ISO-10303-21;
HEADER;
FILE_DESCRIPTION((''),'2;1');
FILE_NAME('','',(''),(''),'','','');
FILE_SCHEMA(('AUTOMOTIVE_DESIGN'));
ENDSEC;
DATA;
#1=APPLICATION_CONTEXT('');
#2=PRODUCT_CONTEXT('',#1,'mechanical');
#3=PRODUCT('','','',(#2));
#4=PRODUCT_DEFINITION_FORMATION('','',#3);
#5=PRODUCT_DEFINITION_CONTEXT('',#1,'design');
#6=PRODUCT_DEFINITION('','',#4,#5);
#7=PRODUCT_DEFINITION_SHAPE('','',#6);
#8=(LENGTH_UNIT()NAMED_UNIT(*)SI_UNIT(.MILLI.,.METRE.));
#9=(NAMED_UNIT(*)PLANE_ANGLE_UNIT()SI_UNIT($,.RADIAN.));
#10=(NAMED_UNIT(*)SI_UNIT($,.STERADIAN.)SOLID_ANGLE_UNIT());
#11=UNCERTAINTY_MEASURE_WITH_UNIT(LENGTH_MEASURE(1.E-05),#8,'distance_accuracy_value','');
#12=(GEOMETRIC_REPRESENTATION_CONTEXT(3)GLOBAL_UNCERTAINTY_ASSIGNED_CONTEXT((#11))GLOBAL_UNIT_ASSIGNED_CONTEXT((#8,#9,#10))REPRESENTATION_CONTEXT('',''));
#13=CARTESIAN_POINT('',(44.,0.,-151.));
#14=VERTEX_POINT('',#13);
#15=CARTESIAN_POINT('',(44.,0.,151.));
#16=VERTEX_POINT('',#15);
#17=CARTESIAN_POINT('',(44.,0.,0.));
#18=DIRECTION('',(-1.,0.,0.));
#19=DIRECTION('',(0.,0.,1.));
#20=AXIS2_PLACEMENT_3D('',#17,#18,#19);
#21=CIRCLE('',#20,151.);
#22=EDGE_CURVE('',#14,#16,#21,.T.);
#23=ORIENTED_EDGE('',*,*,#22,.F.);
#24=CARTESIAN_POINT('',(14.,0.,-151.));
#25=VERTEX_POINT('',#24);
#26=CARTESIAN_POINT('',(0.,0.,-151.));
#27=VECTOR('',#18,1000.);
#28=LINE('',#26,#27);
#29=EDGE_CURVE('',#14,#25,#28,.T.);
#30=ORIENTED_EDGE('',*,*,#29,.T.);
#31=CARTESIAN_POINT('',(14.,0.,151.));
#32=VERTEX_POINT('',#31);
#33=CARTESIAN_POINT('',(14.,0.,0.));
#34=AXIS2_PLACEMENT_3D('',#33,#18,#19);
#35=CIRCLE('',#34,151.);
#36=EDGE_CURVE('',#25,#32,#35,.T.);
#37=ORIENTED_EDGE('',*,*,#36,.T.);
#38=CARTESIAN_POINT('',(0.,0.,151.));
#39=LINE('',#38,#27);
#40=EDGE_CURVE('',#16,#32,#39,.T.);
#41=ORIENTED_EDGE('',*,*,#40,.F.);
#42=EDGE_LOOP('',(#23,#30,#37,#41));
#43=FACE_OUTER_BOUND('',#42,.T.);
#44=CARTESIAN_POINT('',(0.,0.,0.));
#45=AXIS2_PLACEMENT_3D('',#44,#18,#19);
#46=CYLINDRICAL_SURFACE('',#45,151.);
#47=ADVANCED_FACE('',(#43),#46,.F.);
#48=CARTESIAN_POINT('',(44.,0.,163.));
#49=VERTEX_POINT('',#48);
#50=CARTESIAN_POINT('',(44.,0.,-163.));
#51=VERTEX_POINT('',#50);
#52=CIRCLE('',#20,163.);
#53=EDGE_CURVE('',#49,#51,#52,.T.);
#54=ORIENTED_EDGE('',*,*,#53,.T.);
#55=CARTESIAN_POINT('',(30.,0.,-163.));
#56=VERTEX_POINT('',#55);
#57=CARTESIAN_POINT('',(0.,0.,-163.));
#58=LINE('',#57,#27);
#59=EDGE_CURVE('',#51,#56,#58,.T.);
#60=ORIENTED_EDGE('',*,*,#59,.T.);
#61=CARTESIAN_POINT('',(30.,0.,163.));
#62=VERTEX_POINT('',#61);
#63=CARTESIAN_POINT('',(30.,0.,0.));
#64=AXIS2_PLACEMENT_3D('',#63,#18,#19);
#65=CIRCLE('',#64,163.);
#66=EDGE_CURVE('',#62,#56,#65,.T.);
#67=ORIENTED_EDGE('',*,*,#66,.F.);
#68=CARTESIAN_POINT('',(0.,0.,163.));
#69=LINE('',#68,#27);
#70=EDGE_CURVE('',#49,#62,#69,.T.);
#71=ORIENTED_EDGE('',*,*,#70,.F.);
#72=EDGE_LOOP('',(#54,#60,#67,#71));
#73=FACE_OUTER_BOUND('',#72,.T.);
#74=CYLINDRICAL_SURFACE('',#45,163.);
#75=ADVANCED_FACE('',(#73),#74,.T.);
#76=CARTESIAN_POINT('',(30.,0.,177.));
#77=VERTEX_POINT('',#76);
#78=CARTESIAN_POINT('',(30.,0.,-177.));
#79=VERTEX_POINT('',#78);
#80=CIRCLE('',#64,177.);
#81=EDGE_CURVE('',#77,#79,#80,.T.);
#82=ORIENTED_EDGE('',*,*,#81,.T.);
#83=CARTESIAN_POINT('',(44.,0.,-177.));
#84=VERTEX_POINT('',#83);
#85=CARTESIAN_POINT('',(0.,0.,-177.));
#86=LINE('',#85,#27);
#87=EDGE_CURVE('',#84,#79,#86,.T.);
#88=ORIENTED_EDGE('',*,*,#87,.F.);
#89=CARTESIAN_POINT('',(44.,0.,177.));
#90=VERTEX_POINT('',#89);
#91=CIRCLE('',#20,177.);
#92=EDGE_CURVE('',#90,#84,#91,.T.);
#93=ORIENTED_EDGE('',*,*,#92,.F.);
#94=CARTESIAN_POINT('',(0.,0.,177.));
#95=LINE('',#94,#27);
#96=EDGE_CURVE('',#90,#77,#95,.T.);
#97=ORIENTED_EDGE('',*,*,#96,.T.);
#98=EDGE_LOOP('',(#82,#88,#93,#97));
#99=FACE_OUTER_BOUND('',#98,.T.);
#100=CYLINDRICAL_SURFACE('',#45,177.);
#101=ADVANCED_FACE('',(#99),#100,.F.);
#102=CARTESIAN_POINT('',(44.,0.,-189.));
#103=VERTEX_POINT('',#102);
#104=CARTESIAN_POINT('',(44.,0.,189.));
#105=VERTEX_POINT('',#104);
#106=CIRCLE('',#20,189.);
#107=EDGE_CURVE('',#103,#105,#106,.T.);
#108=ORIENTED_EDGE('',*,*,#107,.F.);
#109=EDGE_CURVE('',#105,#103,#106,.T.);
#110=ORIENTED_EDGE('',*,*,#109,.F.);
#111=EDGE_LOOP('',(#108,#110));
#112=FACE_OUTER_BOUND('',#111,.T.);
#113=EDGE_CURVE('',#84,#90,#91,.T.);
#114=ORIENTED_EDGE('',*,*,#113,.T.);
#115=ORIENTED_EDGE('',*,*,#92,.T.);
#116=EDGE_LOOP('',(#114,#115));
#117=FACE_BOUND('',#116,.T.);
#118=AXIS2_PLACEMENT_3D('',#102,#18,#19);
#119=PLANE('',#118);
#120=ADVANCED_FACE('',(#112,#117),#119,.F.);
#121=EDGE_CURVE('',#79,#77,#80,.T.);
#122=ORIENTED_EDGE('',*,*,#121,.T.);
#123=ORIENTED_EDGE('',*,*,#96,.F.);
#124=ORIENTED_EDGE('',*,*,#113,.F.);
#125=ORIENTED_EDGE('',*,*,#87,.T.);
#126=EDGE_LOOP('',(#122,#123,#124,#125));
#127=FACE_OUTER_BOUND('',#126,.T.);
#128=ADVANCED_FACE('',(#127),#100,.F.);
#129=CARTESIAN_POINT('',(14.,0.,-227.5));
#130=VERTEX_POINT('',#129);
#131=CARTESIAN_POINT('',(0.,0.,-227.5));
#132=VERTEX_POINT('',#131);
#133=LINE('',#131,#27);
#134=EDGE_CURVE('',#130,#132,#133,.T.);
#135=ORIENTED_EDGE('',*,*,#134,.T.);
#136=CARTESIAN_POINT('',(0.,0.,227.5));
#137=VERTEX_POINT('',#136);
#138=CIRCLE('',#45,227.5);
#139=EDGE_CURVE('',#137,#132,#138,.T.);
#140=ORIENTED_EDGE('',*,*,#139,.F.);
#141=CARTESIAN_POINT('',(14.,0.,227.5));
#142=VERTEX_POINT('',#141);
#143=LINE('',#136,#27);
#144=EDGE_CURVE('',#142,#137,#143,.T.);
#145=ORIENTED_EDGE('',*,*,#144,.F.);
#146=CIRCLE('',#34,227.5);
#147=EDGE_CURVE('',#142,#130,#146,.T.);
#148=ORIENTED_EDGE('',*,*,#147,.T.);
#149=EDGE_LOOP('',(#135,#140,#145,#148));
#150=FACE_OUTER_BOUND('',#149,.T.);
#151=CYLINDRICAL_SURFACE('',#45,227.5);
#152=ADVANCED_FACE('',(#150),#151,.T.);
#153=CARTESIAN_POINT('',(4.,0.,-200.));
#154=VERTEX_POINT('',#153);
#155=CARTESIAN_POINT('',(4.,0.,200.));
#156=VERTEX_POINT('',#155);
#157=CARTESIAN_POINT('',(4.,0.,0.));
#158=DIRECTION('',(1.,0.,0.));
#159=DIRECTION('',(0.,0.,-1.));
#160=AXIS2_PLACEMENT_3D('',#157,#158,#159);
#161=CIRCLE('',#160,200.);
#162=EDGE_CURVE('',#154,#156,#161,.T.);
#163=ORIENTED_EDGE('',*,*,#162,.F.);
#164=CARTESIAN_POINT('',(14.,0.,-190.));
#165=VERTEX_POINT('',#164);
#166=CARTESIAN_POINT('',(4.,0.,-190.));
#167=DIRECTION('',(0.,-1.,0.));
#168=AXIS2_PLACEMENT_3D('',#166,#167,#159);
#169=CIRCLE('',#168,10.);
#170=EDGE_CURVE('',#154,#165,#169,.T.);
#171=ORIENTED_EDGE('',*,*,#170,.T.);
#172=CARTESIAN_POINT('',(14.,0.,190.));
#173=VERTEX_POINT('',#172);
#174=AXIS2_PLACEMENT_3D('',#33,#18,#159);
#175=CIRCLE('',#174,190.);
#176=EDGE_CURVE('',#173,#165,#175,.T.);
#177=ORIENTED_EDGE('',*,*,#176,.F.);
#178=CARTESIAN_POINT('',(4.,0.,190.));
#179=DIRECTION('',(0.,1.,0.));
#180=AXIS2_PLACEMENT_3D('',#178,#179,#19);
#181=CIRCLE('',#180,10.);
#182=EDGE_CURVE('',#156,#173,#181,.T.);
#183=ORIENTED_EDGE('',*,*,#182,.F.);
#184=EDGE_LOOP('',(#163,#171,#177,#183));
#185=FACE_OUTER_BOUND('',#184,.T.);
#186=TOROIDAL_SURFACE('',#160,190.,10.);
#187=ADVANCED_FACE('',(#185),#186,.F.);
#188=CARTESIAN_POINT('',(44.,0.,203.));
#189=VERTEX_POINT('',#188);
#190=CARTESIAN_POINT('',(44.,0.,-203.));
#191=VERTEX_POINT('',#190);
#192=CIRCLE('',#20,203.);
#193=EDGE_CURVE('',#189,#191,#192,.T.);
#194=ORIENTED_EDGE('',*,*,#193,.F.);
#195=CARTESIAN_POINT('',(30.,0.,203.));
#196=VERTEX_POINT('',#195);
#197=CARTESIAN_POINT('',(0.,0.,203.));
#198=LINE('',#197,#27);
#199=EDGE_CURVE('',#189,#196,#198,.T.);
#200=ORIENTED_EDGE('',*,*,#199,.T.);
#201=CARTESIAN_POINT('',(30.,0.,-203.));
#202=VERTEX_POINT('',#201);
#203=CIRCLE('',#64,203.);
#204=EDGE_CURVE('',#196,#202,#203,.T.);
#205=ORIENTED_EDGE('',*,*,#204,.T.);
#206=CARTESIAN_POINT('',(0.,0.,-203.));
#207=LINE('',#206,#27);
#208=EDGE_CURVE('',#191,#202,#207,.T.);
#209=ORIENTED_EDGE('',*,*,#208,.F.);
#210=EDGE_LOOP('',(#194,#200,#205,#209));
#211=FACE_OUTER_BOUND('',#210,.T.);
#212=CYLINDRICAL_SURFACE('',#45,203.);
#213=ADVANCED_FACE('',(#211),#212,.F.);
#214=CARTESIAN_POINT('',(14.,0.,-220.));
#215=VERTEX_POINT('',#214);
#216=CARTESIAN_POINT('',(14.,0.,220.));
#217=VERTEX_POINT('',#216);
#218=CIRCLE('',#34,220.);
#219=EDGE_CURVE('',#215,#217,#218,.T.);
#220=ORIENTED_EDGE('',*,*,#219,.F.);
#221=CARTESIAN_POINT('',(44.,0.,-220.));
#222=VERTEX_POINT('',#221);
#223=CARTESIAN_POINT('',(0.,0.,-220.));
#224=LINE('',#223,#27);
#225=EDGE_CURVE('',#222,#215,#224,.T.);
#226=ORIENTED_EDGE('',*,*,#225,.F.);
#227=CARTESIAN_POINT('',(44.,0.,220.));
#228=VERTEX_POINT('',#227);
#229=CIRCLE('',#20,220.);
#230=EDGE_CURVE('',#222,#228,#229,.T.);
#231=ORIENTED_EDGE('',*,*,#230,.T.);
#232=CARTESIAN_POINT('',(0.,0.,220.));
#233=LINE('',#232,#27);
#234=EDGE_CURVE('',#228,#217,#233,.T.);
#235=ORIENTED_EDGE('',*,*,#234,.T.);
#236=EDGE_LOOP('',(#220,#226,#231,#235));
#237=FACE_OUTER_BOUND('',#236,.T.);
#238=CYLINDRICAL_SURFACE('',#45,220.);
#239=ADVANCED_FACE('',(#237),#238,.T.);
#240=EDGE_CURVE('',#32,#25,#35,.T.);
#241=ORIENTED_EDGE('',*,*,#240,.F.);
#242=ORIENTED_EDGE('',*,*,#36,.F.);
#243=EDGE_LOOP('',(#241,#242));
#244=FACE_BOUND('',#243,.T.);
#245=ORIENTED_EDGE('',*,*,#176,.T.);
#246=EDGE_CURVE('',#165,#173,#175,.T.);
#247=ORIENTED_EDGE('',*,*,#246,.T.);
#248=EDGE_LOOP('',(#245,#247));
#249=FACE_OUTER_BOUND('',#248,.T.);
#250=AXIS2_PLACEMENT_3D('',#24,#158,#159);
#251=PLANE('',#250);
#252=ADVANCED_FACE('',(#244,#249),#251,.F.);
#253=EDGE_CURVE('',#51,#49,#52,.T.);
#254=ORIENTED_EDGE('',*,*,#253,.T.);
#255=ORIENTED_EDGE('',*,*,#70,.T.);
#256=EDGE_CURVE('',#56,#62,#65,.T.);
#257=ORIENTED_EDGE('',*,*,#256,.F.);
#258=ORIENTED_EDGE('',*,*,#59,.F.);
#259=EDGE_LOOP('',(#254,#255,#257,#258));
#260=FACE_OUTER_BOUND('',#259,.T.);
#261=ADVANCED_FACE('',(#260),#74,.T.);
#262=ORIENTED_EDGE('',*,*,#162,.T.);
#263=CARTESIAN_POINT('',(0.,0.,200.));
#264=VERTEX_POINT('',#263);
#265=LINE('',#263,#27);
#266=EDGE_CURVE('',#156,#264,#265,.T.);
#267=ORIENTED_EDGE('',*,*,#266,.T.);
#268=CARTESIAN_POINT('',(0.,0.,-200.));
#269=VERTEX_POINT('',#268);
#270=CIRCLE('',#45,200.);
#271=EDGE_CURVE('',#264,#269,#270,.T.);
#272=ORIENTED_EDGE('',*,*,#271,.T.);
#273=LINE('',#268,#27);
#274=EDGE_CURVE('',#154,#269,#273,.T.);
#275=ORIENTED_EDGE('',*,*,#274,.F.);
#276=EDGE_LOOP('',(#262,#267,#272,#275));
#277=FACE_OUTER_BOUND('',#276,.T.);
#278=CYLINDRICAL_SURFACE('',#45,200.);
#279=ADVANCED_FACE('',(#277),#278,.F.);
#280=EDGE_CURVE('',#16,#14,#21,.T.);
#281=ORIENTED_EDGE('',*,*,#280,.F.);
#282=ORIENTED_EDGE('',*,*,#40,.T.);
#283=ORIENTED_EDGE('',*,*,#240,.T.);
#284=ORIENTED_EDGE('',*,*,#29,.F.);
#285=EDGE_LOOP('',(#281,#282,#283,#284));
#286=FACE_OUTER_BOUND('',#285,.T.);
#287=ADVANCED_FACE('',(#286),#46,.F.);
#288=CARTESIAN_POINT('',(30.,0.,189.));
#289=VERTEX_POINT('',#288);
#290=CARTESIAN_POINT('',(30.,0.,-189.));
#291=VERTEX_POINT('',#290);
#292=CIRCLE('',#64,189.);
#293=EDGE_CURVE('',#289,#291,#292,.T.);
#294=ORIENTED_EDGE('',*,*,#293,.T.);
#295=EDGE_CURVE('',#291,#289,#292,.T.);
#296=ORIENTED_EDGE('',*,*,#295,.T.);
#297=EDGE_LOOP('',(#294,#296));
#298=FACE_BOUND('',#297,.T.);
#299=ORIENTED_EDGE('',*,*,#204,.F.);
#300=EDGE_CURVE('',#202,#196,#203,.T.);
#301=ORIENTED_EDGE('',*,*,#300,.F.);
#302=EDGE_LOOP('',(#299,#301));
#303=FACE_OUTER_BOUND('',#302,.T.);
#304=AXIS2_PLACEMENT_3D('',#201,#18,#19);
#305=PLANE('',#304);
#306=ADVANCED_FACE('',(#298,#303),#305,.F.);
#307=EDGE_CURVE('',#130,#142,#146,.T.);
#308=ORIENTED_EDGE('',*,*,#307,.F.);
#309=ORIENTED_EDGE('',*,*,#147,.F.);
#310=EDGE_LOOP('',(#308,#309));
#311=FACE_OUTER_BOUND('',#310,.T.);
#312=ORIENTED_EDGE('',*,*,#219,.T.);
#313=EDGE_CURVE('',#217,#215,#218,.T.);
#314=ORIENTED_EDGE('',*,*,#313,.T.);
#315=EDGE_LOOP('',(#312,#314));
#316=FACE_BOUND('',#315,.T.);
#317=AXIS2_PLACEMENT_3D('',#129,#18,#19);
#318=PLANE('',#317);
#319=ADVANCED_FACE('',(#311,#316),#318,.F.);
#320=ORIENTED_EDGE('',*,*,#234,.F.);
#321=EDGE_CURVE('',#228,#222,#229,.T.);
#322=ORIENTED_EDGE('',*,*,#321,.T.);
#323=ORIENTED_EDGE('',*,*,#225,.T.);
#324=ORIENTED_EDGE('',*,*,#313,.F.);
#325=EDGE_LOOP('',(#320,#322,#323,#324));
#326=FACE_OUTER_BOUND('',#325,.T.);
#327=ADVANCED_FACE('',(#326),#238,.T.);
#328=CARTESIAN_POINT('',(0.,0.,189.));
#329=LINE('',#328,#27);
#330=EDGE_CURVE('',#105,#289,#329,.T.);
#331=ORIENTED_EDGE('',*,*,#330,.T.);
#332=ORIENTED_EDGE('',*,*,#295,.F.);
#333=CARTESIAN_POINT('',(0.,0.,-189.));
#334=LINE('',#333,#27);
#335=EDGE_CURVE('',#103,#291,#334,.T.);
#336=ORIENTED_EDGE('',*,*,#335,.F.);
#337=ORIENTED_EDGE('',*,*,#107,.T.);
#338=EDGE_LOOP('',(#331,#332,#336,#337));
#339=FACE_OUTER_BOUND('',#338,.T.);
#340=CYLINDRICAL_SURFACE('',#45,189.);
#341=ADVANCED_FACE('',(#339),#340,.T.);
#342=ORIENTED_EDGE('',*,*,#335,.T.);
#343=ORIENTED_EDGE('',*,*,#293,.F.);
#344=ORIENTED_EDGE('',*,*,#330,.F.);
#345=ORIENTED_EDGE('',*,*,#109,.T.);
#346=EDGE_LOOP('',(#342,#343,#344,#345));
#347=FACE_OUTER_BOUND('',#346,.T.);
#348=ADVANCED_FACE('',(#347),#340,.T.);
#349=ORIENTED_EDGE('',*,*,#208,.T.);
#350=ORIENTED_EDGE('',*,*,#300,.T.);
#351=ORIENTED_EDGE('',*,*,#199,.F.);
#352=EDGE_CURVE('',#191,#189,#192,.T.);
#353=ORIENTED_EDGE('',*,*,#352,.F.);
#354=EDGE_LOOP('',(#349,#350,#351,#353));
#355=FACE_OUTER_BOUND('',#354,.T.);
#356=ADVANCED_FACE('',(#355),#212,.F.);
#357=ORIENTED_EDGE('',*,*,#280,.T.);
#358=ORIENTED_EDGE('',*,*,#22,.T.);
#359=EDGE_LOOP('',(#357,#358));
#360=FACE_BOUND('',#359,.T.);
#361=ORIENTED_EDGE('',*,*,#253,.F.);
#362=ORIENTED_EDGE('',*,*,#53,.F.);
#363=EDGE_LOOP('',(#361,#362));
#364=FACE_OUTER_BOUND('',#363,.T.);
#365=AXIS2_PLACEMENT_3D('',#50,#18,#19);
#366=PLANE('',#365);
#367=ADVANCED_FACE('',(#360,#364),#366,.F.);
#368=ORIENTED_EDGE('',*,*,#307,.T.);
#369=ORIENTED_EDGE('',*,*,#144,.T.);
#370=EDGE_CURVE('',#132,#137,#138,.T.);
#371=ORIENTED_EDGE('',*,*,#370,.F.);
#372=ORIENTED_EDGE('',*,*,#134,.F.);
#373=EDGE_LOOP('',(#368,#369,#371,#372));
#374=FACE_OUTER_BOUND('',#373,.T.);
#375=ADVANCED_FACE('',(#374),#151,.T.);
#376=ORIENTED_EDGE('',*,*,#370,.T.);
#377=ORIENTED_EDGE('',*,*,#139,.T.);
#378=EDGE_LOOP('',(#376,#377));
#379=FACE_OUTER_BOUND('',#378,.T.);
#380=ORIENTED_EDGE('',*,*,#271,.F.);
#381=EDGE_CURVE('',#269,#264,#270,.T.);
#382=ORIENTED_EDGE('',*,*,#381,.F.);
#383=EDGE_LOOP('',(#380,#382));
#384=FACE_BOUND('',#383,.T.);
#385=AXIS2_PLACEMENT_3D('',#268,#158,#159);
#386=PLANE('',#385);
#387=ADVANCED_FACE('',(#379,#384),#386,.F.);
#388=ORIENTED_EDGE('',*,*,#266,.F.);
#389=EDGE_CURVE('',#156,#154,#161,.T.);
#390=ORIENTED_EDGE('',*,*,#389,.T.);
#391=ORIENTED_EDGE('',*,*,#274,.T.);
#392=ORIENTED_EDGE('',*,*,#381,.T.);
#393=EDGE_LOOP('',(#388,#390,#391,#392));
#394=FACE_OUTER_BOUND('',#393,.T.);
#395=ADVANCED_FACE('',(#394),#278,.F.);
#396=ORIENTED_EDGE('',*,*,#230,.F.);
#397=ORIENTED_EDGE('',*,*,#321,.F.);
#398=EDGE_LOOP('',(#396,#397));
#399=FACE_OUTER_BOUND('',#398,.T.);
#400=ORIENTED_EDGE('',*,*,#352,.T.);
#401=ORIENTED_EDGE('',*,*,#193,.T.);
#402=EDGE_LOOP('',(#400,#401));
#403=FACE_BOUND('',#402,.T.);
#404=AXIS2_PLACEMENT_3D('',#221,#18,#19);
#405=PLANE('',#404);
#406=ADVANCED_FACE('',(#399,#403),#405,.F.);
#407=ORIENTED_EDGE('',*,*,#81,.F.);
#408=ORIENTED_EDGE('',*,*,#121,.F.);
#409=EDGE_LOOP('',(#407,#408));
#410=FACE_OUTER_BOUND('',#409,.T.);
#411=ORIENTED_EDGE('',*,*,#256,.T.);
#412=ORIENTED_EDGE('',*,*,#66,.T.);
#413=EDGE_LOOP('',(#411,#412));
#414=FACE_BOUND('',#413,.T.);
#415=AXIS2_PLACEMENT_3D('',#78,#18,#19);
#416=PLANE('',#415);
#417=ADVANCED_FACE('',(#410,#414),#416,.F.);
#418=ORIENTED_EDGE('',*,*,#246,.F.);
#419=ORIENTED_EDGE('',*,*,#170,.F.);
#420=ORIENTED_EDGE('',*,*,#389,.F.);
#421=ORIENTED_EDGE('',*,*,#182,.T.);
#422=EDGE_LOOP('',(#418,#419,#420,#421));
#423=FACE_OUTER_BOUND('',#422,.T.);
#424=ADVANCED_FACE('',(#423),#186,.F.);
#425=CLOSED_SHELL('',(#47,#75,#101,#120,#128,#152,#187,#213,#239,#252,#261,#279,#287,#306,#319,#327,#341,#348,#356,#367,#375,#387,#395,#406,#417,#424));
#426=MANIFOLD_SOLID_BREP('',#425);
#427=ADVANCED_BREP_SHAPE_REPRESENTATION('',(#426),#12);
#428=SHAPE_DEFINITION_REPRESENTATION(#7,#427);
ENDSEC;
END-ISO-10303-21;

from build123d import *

# Parameters (mm, degrees)
FILLET1_R = 10


with BuildPart() as part:
    # Sketch1 → Revolve1 (revolve)
    with BuildSketch(Plane(origin=(0, 0, 0), x_dir=(1, 0, 0), z_dir=(0, 1, 0)), mode=Mode.PRIVATE) as revolve1_sk:
        Polygon((0, 200), (0, 227.5), (14, 227.5), (14, 220), (44, 220), (44, 203), (30, 203), (30, 189), (44, 189), (44, 177), (30, 177), (30, 163), (44, 163), (44, 151), (14, 151), (14, 200), align=None)
    revolve(revolve1_sk.sketch.rotate(Axis((0, 0, 0), (1, 0, 0)), 180), axis=Axis((0, 0, 0), (1, 0, 0)))

    # Fillet1
    fillet1_edges = [part.edges().sort_by_distance(p)[0] for p in [
        (14, 0, -200),
    ]]
    fillet(fillet1_edges, radius=FILLET1_R)


solid = part.part
